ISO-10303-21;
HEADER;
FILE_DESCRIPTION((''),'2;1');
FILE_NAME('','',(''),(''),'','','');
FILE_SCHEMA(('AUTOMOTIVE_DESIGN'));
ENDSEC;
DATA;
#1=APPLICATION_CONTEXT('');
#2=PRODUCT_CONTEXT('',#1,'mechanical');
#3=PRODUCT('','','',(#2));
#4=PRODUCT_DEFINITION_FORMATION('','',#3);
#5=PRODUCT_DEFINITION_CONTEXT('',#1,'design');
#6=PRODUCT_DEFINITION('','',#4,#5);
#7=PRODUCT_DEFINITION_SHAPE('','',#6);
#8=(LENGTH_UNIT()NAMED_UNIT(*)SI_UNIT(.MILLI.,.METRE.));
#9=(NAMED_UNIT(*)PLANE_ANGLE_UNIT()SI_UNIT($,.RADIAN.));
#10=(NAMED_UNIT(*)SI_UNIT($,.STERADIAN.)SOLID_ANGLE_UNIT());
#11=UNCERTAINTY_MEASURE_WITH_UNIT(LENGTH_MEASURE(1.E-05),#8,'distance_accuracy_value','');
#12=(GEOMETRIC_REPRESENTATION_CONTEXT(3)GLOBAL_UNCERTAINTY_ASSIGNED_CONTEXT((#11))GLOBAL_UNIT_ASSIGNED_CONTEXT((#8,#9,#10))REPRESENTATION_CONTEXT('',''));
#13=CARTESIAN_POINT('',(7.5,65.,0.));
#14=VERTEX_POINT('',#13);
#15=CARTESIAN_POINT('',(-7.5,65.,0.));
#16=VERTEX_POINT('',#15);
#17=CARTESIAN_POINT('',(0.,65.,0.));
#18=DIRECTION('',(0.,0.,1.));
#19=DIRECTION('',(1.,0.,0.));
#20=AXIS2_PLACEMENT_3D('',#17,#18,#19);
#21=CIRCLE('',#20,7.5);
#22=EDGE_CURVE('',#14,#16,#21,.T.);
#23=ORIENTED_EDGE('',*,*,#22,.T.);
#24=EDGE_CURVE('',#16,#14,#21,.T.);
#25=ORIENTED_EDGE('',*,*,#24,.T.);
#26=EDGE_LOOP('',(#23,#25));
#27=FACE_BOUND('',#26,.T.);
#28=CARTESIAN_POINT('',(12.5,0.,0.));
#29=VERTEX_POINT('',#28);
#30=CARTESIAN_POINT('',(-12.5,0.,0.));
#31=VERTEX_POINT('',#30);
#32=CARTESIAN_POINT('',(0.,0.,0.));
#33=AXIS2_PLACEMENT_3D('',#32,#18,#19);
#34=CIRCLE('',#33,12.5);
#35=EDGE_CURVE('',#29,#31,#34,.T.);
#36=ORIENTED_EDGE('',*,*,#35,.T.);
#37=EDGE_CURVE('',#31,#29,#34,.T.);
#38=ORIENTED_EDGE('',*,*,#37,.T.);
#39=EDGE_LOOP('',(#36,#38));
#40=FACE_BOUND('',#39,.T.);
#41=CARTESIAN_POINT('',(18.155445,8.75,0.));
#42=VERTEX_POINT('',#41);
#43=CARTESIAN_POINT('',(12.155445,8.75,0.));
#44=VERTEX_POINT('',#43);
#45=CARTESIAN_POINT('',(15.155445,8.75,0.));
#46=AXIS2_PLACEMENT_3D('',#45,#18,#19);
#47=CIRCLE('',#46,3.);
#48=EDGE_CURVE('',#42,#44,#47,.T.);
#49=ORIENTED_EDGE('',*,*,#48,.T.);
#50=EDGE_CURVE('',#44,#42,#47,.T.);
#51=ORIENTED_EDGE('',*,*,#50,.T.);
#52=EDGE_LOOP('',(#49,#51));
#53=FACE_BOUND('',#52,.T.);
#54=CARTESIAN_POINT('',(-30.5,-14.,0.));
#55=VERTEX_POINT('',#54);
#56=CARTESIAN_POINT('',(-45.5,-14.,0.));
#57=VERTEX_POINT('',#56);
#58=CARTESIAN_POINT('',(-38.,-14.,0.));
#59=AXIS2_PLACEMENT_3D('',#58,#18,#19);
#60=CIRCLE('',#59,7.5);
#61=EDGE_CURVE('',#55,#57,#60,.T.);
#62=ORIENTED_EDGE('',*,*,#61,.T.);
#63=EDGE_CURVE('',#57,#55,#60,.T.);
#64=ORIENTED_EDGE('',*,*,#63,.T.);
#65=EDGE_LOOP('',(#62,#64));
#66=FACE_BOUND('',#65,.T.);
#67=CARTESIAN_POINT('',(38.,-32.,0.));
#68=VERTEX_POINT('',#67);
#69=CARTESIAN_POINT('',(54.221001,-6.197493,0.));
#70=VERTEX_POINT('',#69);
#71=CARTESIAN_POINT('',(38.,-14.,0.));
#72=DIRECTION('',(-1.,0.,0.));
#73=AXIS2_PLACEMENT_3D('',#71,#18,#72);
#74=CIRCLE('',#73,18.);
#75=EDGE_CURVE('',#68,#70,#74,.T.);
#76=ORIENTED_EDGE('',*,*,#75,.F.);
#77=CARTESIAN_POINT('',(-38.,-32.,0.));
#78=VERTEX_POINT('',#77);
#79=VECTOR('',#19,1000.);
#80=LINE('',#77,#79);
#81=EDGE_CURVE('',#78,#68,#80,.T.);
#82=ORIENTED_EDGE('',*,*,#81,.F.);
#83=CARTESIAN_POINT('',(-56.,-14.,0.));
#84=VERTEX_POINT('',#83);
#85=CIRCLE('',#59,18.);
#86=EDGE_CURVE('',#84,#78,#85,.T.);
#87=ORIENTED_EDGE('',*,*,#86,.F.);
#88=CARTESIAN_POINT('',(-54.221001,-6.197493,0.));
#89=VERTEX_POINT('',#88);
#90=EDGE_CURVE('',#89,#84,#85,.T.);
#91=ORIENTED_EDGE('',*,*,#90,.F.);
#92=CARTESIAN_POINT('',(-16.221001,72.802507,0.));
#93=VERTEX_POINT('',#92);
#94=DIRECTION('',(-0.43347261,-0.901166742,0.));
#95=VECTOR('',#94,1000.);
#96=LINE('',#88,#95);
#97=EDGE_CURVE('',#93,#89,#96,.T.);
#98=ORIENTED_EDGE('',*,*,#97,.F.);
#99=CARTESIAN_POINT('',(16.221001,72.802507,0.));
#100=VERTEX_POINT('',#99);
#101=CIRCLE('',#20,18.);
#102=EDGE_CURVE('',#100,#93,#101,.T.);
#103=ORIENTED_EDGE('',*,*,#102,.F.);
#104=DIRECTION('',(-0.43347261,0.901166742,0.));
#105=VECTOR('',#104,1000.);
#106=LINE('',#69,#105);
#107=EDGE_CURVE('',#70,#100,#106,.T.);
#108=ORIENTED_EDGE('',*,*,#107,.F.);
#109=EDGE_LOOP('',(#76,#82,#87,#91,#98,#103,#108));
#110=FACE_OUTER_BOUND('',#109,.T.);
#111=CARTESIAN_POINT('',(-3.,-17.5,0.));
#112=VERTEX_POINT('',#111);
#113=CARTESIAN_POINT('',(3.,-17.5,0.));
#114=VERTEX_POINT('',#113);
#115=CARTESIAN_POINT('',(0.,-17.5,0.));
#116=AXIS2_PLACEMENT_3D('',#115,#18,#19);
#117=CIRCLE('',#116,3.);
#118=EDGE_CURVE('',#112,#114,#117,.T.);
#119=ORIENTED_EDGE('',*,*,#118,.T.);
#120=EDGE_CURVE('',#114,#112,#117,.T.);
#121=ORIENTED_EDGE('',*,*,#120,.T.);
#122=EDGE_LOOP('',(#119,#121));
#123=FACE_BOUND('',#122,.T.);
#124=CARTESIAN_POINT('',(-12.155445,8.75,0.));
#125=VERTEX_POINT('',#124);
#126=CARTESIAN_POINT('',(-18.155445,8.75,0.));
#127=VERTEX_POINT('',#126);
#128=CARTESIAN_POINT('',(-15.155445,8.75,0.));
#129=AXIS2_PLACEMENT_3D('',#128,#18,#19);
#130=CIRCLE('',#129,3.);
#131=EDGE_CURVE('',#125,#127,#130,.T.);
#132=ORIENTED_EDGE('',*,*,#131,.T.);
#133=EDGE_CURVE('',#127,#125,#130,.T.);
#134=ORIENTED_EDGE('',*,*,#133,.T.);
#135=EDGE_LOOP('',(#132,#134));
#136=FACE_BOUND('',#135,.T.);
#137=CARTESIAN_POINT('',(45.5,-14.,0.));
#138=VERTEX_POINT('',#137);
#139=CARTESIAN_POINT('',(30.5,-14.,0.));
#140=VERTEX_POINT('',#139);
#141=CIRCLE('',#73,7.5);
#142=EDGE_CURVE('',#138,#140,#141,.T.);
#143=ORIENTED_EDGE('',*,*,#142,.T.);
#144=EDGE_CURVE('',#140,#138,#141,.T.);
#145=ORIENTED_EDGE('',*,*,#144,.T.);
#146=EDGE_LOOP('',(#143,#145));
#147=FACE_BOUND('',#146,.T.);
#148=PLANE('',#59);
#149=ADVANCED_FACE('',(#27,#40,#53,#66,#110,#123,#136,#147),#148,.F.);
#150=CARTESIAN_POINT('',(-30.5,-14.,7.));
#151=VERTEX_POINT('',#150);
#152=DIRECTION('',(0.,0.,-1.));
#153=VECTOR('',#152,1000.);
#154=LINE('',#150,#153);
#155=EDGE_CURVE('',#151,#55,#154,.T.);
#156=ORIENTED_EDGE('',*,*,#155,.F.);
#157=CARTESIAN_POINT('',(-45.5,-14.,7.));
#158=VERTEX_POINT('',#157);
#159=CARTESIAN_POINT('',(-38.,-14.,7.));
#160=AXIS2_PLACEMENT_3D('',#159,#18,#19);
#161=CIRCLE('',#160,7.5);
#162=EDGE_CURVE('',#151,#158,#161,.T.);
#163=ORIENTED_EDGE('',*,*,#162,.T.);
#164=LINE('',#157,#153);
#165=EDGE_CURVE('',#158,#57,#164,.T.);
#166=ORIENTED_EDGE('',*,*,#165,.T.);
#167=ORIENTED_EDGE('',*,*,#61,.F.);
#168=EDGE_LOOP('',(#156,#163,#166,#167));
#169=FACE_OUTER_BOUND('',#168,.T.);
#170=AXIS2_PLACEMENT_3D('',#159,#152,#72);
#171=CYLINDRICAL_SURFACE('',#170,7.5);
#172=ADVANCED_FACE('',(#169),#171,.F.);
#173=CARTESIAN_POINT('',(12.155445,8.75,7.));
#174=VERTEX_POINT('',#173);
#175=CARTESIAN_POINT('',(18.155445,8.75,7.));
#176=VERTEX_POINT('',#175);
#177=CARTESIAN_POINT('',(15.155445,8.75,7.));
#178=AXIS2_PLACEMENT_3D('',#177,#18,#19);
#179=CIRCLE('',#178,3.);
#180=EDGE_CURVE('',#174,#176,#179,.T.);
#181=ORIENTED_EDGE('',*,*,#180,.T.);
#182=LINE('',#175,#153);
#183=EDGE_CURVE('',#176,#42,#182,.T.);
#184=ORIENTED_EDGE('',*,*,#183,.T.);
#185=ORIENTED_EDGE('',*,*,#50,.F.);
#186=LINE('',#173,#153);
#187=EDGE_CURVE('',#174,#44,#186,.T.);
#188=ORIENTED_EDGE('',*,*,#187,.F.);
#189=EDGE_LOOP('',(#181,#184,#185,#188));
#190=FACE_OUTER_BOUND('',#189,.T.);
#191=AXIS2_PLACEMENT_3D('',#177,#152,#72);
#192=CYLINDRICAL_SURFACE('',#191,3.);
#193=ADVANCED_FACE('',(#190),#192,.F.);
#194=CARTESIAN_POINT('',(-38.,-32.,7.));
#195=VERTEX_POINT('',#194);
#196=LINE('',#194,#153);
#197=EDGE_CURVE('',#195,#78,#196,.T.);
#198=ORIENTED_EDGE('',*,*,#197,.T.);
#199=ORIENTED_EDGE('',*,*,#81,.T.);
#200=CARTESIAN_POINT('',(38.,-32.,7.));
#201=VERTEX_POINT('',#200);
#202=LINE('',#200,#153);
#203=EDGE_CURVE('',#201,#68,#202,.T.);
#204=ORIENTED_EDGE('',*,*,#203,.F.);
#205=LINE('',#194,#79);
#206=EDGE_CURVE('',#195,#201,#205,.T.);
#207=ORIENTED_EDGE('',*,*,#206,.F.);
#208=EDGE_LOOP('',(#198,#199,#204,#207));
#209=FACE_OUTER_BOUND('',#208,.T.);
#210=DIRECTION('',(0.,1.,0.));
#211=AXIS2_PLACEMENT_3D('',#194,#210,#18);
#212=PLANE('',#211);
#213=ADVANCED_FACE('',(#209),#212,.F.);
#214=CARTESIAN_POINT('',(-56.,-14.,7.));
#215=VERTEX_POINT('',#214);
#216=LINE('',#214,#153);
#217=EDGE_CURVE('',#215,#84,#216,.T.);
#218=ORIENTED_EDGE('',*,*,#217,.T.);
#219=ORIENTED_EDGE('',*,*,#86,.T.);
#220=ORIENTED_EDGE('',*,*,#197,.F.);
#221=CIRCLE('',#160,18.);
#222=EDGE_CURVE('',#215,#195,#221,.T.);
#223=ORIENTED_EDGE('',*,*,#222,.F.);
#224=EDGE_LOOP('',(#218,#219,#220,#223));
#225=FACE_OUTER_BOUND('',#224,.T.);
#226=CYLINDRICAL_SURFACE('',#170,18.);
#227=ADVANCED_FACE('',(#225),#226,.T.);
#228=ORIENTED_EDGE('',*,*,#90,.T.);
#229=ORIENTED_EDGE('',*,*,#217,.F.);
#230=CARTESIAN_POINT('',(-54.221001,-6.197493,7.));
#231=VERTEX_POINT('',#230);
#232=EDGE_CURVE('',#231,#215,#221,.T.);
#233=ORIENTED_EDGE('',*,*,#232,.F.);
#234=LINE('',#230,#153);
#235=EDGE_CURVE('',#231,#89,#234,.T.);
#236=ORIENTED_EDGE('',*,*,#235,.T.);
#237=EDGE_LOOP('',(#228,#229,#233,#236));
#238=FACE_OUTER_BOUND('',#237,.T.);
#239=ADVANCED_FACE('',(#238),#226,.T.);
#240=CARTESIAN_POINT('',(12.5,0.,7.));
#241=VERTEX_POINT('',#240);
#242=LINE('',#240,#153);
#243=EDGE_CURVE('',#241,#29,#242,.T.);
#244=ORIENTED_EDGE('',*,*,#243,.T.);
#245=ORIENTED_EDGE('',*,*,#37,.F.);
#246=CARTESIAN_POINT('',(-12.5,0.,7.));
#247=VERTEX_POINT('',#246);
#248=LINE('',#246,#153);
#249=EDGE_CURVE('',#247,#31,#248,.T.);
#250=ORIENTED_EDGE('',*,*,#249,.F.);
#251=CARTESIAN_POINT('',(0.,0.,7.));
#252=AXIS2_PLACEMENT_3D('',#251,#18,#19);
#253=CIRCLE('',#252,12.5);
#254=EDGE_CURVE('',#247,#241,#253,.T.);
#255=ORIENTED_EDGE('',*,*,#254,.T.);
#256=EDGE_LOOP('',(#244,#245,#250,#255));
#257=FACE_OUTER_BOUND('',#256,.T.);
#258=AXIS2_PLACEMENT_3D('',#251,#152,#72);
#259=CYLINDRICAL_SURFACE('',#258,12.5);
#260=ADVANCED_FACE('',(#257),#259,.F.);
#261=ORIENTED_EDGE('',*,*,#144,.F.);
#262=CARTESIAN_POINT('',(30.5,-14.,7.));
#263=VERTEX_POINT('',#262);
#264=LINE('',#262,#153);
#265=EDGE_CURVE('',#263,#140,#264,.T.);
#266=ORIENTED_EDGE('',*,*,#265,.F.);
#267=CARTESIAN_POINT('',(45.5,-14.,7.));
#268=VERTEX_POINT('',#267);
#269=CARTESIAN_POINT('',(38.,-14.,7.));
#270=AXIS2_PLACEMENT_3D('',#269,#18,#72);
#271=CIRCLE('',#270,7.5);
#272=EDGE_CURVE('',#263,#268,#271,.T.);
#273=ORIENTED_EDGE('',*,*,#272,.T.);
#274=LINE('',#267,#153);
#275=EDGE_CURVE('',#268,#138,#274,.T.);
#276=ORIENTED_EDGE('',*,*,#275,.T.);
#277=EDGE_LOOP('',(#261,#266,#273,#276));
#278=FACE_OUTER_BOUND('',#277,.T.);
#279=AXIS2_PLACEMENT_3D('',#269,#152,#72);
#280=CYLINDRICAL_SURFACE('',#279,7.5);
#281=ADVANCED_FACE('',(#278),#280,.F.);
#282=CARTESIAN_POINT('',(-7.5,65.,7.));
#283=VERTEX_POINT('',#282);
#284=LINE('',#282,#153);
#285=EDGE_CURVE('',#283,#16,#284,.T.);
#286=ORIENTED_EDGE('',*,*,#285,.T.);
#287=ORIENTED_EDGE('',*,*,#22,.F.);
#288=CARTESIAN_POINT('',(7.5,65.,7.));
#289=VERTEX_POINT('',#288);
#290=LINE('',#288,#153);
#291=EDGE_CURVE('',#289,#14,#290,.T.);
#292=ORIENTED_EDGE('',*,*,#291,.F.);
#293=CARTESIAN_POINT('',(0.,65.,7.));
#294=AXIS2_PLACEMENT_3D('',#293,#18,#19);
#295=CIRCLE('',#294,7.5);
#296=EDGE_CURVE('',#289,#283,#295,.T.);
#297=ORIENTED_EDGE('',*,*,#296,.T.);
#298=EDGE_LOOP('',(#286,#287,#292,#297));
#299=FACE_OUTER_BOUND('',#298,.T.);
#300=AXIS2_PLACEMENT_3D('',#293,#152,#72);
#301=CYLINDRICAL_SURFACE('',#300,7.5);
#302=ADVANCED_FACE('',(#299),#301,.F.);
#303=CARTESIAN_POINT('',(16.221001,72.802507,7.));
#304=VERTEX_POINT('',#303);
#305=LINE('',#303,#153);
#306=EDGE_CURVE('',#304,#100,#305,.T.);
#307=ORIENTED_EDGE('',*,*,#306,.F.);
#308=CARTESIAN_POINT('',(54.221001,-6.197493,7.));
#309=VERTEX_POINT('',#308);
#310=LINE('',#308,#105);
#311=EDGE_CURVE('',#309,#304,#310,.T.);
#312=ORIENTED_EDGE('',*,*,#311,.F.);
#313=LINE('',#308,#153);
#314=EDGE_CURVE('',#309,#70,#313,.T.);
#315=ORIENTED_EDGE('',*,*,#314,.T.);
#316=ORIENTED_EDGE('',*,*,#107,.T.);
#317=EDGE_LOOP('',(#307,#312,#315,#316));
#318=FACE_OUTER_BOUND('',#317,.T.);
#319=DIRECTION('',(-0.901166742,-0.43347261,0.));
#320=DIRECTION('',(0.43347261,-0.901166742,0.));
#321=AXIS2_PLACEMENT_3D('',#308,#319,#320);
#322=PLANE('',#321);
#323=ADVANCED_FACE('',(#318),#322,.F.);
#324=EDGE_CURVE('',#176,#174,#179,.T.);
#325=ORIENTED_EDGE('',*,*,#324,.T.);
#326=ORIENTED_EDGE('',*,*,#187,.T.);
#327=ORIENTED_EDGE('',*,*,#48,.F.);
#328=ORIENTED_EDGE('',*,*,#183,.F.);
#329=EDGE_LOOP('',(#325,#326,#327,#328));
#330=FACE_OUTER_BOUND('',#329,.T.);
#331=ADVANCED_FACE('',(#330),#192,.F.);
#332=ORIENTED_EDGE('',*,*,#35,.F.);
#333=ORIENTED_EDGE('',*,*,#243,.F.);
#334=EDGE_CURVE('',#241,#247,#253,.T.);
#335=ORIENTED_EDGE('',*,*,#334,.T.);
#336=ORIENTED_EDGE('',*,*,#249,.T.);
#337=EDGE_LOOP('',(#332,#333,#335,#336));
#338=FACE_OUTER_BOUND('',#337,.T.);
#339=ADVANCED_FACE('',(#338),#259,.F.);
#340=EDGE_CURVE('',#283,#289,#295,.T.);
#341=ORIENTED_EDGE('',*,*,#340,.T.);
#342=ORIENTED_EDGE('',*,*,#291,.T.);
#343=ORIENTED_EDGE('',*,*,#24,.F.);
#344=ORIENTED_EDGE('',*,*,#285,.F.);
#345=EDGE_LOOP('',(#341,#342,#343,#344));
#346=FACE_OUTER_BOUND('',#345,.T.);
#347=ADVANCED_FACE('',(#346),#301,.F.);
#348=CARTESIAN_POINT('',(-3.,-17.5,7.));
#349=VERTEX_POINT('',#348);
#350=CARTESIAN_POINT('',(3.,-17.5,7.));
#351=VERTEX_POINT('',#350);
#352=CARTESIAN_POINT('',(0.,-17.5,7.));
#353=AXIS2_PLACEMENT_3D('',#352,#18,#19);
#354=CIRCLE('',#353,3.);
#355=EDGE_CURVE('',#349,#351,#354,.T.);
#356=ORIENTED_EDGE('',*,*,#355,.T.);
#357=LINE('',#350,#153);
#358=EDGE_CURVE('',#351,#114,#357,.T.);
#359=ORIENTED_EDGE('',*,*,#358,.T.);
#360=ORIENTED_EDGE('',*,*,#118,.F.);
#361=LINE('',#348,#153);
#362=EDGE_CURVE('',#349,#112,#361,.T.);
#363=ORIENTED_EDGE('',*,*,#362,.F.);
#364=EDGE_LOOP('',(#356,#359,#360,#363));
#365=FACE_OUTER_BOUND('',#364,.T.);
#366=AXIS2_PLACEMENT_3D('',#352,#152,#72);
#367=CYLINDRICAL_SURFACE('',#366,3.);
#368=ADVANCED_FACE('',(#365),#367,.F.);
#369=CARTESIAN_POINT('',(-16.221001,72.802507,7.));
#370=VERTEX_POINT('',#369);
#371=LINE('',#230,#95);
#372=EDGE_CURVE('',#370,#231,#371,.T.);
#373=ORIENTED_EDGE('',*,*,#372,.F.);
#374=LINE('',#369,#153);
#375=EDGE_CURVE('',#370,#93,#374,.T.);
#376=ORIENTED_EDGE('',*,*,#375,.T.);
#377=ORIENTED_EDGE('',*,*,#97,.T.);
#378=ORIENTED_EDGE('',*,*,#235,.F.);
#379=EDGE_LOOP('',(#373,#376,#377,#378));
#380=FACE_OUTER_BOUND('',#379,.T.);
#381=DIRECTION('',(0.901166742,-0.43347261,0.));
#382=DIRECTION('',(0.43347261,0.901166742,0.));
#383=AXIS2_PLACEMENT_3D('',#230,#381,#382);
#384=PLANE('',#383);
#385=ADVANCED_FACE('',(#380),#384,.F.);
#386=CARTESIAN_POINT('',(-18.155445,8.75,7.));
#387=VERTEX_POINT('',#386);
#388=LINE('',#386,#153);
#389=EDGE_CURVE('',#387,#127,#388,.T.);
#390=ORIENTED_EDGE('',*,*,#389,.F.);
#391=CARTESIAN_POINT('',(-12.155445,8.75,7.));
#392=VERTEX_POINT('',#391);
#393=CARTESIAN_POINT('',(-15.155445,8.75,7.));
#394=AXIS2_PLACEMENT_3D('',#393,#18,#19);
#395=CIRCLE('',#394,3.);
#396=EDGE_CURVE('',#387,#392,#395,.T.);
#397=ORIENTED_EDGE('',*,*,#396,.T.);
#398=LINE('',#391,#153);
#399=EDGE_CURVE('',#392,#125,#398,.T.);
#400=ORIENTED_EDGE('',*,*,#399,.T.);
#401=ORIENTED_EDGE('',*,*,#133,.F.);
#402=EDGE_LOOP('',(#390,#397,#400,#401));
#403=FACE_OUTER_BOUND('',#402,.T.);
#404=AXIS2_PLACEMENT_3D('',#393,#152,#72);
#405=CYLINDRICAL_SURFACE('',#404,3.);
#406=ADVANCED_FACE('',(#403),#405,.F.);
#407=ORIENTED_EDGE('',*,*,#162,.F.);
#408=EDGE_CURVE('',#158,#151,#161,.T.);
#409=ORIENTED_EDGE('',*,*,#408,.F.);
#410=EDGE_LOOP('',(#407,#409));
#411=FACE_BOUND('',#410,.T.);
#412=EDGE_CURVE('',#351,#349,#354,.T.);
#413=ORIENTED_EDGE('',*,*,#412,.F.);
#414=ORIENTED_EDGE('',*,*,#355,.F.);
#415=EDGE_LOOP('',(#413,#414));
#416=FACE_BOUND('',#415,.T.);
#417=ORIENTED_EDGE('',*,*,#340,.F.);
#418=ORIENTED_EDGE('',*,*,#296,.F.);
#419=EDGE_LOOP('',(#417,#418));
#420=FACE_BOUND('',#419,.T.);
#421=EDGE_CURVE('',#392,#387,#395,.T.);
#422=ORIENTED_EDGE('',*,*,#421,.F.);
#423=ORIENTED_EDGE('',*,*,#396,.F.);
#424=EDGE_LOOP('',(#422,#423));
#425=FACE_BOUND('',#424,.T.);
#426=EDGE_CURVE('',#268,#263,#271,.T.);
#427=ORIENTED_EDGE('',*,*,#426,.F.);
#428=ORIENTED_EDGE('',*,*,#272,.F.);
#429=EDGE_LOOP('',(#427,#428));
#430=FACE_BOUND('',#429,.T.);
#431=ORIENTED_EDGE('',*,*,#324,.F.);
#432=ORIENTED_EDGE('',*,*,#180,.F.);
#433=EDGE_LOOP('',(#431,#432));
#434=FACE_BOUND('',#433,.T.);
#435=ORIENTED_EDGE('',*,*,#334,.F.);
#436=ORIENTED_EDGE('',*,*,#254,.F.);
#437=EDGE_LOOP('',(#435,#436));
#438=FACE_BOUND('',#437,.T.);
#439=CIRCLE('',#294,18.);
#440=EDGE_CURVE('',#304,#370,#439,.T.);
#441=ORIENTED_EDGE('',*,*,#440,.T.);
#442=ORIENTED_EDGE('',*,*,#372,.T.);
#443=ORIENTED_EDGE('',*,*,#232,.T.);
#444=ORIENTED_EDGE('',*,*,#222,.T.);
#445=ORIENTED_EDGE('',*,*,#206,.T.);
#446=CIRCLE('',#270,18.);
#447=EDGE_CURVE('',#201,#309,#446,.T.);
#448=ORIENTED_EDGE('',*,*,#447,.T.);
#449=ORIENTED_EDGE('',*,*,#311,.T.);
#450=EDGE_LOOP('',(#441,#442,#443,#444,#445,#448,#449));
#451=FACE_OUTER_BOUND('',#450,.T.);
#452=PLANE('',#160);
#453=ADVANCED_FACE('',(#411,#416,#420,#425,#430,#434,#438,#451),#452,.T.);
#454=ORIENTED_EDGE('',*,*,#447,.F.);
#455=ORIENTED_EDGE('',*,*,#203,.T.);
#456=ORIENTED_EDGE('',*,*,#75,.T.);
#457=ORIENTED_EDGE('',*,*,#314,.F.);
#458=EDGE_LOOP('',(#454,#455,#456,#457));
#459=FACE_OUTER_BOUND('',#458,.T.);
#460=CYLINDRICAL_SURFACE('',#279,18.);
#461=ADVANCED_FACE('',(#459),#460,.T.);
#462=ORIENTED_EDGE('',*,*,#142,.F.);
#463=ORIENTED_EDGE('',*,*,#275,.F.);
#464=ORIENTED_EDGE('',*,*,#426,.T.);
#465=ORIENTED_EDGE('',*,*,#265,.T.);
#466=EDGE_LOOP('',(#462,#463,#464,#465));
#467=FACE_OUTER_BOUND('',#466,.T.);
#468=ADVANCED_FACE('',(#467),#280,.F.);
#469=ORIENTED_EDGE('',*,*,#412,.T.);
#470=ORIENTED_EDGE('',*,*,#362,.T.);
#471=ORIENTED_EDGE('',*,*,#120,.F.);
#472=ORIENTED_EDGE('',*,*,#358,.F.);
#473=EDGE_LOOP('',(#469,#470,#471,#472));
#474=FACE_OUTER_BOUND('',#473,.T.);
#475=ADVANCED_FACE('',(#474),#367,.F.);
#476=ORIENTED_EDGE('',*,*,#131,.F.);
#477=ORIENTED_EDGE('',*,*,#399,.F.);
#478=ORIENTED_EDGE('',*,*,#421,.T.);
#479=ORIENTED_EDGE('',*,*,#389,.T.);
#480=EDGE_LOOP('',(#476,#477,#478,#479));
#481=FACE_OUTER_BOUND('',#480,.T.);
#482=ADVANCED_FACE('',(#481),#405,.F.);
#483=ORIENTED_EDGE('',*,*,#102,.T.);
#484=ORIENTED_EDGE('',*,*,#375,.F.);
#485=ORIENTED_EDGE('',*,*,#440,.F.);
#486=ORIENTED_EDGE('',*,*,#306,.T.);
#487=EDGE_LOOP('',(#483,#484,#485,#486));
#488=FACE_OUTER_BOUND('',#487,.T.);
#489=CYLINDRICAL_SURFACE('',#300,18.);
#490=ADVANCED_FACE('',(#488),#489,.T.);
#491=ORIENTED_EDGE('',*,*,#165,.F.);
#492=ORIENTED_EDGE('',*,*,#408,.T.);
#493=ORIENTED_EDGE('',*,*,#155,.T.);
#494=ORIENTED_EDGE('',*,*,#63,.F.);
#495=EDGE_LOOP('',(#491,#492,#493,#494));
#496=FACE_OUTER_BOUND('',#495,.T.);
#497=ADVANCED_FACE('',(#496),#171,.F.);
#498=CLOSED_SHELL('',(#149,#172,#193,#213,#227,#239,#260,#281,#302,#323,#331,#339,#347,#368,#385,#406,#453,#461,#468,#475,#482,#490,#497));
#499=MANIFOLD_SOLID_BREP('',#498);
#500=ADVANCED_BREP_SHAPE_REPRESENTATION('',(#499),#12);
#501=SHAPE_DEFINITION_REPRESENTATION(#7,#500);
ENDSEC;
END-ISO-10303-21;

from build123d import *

# Parameters (mm, degrees)
PLATE_PROFILE_R         = 12.5
PLATE_PROFILE_R_2       = 3
PLATE_PROFILE_R_3       = 7.5
SUPPORT_PLATE_7MM_DEPTH = 7


with BuildPart() as part:
    # Plate Profile → Support Plate 7mm (new body)
    with BuildSketch(Plane.XY):
        with BuildLine():
            Line((-38, -32), (38, -32))
            ThreePointArc((38, -32), (53.238850443, -23.580054133), (54.221001351, -6.197493021))
            Line((54.221001351, -6.197493021), (16.221001351, 72.802506979))
            ThreePointArc((16.221001351, 72.802506979), (0, 83), (-16.221001351, 72.802506979))
            Line((-16.221001351, 72.802506979), (-54.221001351, -6.197493021))
            ThreePointArc((-54.221001351, -6.197493021), (-53.238850443, -23.580054133), (-38, -32))
        make_face()
        Circle(PLATE_PROFILE_R, mode=Mode.SUBTRACT)
        with Locations((0, -17.5)):
            Circle(PLATE_PROFILE_R_2, mode=Mode.SUBTRACT)
        with Locations((-15.155444566, 8.75)):
            Circle(PLATE_PROFILE_R_2, mode=Mode.SUBTRACT)
        with Locations((15.155444566, 8.75)):
            Circle(PLATE_PROFILE_R_2, mode=Mode.SUBTRACT)
        with Locations((-38, -14)):
            Circle(PLATE_PROFILE_R_3, mode=Mode.SUBTRACT)
        with Locations(Location((38, -14, 0), (0, 0, 180))):
            Circle(PLATE_PROFILE_R_3, mode=Mode.SUBTRACT)
        with Locations((0, 65)):
            Circle(PLATE_PROFILE_R_3, mode=Mode.SUBTRACT)
    extrude(amount=SUPPORT_PLATE_7MM_DEPTH)


solid = part.part
